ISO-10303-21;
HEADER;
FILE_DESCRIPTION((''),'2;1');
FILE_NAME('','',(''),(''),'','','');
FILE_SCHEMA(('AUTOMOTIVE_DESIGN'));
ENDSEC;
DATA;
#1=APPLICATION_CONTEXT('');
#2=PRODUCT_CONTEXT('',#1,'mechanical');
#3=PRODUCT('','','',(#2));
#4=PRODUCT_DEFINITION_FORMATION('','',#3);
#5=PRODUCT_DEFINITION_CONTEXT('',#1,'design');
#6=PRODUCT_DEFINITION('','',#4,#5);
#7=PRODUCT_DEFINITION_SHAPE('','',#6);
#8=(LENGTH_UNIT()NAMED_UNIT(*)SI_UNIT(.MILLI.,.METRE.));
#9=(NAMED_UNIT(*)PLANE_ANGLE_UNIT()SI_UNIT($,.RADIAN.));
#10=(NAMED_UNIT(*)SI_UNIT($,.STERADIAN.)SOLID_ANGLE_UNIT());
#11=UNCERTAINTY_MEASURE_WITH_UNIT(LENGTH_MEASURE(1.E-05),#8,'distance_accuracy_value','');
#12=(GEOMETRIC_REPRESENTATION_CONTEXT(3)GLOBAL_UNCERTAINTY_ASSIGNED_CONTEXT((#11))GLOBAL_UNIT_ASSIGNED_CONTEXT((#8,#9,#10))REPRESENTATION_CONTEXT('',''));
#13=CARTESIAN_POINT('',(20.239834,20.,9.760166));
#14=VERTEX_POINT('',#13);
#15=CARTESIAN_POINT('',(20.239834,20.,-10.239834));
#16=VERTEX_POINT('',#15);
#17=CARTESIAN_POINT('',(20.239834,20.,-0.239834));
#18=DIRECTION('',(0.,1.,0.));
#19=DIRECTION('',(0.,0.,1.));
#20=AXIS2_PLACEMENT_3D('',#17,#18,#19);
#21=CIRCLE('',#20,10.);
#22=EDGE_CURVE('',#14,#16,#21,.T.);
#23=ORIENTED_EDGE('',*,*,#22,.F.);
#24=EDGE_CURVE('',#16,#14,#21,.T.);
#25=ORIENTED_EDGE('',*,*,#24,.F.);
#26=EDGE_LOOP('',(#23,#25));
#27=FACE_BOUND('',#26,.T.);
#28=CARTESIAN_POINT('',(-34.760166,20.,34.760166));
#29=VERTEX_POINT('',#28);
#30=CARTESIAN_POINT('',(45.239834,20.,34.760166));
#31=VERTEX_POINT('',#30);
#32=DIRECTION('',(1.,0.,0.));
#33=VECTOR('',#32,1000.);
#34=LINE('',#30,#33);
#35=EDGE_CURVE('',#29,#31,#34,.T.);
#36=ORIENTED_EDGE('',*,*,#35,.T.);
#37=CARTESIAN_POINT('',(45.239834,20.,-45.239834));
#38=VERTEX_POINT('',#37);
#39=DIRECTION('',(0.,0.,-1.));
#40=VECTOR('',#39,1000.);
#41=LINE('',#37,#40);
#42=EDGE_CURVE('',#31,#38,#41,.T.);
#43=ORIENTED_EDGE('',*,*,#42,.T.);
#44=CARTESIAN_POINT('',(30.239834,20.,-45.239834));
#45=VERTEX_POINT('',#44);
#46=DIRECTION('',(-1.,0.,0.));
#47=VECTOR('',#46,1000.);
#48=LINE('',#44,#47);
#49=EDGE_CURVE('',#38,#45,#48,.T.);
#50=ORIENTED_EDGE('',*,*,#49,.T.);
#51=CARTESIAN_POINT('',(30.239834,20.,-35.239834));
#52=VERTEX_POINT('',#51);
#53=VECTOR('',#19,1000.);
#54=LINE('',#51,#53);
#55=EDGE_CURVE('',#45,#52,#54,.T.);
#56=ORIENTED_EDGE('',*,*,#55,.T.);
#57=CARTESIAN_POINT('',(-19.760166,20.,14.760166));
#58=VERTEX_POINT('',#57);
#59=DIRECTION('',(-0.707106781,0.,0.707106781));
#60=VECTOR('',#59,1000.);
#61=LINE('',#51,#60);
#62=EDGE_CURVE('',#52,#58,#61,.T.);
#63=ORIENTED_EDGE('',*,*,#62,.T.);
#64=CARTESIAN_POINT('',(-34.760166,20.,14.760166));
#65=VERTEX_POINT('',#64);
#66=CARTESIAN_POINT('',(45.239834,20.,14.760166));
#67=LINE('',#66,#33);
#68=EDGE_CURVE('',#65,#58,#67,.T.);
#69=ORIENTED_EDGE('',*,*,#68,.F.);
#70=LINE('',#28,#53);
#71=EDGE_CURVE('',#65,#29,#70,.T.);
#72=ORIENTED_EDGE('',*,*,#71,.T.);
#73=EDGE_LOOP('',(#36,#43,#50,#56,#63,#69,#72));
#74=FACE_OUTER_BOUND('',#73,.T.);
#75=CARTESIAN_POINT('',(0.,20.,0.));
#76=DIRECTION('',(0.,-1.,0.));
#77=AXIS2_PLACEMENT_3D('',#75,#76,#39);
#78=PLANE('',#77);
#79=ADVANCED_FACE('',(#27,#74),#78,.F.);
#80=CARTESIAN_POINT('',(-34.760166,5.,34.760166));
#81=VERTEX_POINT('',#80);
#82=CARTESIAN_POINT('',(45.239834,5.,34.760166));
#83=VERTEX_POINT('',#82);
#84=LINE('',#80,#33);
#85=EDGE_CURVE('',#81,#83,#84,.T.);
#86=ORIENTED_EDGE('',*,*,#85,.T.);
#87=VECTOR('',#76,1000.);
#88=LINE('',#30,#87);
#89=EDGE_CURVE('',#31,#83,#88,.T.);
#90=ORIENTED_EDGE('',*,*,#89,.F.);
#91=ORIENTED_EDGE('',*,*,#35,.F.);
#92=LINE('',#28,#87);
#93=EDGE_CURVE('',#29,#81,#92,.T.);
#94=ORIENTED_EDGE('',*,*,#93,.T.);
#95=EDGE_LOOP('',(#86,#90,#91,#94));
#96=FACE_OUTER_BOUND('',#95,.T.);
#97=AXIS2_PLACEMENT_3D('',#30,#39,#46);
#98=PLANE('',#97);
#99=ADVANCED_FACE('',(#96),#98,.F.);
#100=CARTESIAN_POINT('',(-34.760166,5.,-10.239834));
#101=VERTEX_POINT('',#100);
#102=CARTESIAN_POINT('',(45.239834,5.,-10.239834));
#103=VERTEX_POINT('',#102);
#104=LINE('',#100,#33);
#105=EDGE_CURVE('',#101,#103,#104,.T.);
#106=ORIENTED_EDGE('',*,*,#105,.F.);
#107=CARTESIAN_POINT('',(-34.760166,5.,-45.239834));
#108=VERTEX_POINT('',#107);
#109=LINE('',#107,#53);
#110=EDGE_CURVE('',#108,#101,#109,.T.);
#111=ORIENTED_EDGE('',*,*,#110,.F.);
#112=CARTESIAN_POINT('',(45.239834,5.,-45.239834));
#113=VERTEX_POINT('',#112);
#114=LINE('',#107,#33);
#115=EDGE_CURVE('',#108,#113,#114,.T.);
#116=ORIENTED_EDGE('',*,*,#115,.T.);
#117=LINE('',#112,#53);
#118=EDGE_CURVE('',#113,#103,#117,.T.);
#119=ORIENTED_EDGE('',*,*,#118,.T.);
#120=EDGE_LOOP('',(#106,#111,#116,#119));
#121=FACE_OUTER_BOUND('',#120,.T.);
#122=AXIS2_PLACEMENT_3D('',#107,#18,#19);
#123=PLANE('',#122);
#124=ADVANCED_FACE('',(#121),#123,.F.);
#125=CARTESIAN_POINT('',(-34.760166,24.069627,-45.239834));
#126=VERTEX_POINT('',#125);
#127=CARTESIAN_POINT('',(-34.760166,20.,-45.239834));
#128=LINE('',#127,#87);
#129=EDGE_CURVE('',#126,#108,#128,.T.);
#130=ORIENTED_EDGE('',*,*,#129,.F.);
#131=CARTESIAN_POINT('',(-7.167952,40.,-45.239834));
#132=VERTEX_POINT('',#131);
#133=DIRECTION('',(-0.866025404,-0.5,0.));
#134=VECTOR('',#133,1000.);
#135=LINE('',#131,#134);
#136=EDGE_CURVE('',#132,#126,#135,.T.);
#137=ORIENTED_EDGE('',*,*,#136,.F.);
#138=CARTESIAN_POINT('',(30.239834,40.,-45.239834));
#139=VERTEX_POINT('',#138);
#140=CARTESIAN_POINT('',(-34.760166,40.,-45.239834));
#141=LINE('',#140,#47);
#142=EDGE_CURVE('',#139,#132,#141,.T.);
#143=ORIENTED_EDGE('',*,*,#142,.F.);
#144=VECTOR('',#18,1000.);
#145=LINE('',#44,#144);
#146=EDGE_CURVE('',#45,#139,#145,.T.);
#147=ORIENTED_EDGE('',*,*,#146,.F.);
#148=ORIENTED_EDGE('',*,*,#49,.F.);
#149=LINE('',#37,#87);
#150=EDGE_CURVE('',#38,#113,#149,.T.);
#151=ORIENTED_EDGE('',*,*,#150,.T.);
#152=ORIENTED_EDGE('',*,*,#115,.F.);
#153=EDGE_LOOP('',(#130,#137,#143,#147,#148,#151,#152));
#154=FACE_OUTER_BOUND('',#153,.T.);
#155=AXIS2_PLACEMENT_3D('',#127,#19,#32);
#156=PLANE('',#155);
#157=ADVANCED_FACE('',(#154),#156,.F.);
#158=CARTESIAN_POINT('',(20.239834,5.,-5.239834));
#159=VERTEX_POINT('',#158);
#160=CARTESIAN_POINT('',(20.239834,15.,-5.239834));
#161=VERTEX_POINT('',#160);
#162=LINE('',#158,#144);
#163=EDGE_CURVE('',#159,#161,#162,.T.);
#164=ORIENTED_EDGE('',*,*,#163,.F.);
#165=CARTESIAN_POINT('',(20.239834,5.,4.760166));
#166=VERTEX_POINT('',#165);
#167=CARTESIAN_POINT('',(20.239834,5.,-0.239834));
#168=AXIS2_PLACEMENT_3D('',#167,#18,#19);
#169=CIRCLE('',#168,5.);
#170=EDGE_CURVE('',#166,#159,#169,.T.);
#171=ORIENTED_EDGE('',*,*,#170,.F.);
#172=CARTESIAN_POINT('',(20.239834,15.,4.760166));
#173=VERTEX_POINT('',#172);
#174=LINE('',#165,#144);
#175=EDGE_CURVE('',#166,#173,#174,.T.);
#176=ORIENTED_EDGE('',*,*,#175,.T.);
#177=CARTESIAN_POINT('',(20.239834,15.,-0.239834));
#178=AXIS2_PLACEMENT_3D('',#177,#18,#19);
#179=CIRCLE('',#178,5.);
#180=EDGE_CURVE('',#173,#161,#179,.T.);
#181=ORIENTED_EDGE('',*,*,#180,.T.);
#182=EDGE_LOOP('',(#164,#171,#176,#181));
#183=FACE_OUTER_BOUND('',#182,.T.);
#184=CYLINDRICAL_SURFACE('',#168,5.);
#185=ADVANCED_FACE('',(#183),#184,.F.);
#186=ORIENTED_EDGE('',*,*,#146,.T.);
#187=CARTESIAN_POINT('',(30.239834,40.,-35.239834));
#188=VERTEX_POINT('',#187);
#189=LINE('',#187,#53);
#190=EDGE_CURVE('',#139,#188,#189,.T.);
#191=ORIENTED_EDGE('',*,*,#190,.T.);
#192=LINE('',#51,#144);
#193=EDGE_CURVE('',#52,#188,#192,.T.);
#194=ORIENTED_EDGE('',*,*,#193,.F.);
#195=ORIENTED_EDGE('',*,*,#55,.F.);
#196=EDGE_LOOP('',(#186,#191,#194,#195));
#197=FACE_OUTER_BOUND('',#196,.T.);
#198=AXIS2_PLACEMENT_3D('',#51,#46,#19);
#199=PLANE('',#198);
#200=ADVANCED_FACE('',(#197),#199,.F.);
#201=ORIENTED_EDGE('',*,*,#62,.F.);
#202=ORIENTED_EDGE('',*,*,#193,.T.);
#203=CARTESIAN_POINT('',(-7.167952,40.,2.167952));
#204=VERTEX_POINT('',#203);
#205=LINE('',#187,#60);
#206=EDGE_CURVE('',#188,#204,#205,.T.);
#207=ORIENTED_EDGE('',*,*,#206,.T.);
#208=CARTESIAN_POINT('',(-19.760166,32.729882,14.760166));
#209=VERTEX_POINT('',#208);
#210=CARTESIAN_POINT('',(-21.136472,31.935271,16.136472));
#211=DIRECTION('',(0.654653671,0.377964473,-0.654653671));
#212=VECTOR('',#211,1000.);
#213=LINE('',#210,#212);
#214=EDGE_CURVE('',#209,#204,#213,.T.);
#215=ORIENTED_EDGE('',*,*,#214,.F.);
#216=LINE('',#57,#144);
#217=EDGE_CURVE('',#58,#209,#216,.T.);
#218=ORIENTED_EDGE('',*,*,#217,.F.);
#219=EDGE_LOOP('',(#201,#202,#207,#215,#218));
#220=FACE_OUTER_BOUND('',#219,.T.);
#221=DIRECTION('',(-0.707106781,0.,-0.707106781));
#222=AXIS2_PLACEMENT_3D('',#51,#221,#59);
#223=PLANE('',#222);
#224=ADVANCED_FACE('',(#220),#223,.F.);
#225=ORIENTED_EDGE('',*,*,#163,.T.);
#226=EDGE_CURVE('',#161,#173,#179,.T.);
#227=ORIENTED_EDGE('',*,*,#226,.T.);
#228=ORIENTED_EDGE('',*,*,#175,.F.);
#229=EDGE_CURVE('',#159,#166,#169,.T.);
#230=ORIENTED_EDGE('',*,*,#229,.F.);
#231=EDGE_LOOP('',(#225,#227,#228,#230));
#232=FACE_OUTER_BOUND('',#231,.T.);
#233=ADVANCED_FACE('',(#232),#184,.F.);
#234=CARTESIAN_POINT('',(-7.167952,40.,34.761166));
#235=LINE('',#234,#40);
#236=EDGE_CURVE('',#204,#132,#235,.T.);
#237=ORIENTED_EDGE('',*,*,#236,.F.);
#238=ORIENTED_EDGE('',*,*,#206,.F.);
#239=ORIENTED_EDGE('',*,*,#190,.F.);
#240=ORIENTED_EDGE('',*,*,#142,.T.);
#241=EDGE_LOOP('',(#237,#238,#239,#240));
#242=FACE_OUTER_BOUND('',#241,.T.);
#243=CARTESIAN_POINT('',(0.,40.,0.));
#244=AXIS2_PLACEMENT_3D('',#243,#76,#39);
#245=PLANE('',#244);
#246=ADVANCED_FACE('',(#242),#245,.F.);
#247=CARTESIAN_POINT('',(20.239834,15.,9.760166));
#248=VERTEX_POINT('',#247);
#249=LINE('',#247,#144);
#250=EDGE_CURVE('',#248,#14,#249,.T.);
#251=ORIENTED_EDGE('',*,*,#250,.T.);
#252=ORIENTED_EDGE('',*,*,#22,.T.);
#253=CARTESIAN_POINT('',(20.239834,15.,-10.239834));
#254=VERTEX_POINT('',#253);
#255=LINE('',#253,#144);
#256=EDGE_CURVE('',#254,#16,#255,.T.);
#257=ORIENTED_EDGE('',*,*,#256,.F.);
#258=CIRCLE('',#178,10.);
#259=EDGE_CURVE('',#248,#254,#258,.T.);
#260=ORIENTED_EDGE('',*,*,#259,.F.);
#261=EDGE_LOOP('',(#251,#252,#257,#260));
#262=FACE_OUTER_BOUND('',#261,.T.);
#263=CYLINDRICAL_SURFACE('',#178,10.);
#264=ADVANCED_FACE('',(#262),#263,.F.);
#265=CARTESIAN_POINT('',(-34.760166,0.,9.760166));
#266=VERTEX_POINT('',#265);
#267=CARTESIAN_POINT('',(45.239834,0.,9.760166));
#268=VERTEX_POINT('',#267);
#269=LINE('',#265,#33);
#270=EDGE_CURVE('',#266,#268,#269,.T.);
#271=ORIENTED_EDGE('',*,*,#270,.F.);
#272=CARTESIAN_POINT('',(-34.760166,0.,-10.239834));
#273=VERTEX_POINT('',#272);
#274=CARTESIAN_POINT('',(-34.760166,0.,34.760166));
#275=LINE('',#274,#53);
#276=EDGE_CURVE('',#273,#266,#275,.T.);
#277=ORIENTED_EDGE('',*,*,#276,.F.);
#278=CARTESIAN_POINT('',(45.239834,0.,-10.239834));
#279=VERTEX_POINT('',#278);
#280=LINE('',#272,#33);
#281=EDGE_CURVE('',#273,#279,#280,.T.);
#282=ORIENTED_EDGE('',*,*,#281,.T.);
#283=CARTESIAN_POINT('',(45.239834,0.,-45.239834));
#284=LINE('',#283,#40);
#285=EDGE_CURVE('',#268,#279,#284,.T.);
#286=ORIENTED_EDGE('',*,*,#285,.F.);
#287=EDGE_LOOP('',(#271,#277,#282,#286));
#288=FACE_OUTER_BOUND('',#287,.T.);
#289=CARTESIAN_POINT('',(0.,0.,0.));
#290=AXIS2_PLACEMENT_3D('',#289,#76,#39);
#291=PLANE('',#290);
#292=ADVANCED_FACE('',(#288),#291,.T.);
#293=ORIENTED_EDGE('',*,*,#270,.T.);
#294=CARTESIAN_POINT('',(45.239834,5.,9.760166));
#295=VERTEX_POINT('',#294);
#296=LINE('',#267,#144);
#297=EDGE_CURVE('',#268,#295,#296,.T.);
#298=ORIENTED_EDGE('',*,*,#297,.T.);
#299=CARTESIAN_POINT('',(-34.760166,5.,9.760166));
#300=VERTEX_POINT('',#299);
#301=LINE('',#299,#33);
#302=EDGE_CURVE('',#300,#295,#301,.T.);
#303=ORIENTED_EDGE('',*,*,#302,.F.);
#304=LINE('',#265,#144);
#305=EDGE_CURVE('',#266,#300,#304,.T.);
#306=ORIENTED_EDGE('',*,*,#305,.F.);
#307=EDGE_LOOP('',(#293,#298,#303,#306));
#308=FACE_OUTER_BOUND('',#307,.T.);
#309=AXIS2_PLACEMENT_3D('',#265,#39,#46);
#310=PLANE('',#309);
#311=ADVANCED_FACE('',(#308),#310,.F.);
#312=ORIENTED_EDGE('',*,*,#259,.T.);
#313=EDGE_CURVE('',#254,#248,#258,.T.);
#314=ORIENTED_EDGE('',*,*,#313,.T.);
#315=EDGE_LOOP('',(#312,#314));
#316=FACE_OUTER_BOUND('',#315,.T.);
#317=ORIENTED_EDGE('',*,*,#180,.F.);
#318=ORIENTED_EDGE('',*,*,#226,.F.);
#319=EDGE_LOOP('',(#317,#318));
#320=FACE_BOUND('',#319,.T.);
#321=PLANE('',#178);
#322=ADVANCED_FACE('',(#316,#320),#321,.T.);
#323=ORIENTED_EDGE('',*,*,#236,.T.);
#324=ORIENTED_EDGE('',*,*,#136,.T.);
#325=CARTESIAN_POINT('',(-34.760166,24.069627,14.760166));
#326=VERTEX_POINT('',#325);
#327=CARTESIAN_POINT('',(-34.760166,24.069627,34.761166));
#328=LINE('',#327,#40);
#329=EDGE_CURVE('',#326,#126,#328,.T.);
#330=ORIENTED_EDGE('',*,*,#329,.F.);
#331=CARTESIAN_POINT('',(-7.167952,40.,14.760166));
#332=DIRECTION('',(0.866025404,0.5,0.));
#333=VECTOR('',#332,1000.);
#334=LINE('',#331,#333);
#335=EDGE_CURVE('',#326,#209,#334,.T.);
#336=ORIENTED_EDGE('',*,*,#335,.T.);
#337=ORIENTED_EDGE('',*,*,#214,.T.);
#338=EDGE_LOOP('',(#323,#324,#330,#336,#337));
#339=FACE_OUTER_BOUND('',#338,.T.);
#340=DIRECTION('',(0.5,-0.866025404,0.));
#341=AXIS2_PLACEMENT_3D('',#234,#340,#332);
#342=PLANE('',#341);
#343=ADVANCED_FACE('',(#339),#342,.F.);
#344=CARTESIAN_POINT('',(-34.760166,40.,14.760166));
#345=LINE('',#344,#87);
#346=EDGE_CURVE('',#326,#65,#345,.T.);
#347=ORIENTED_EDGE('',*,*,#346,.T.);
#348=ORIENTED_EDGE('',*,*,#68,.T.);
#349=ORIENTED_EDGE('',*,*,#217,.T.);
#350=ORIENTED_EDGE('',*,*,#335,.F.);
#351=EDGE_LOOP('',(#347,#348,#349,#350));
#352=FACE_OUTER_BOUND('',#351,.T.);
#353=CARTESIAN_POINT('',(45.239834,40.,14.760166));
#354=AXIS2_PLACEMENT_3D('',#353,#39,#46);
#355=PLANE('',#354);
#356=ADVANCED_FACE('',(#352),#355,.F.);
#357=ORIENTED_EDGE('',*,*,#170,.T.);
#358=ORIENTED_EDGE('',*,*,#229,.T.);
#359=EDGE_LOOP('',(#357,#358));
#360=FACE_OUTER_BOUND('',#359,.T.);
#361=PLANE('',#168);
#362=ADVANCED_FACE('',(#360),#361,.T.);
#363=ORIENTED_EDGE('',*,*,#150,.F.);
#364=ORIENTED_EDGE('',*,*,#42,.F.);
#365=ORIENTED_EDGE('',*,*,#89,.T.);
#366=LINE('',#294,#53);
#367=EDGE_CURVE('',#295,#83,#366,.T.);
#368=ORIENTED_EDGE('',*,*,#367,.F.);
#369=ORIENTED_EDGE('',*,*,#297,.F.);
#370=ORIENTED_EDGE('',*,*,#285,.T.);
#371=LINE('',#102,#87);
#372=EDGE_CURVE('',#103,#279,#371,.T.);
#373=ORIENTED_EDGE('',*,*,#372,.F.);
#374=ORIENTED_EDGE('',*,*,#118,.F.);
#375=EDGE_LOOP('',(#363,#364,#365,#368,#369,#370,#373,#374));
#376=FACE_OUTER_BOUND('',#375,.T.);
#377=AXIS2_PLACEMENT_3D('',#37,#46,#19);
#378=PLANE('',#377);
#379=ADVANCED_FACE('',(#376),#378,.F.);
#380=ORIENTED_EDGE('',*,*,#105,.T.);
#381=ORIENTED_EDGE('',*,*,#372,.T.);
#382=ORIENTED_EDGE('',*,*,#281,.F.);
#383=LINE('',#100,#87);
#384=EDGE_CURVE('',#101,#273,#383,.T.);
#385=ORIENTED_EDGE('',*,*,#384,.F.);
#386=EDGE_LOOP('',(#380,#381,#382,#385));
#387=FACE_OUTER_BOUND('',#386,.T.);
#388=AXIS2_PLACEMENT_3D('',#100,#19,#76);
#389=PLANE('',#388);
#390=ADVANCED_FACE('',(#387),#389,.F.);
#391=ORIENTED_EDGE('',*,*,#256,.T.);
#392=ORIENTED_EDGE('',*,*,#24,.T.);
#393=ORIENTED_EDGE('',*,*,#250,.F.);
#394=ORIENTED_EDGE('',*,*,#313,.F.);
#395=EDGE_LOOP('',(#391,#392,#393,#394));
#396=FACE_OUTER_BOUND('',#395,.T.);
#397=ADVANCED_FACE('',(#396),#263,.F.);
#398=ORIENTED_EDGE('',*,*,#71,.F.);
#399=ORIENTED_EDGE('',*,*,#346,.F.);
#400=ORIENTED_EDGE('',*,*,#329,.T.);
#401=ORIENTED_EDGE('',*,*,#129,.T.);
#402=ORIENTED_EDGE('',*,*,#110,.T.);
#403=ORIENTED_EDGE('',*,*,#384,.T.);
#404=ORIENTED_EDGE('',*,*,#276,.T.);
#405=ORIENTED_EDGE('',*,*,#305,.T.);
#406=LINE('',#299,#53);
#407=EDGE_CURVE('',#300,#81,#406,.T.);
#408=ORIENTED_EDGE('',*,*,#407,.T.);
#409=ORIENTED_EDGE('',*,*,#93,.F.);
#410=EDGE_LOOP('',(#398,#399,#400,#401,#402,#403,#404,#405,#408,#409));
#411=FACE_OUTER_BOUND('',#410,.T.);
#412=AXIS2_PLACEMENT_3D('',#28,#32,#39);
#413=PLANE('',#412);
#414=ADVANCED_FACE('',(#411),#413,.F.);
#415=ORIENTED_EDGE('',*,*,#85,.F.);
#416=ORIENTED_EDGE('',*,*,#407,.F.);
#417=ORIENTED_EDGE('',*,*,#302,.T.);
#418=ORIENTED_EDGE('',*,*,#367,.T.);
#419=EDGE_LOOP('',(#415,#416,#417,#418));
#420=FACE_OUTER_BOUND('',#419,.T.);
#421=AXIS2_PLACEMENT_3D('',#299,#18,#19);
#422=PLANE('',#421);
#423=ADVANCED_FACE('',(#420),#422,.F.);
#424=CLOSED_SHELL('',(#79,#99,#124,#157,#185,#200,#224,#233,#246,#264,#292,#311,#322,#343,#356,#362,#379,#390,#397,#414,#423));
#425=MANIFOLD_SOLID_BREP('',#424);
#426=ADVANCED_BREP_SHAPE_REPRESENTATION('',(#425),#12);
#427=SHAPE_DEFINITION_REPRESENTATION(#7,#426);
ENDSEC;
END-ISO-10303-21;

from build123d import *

# Parameters (mm, degrees)
BASE_PLATE_SKETCH_W          = 80
BASE_PLATE_SKETCH_H          = 80
BASE_PLATE_80X80X20_DEPTH    = 20
BOTTOM_SLOT_SKETCH_W         = 25
BOTTOM_SLOT_SKETCH_H         = 5
BOTTOM_SLOT_SKETCH_W_2       = 35
BOTTOM_SLOT_DEPTH            = 80
RAISED_BLOCK_SKETCH_W        = 80
RAISED_BLOCK_SKETCH_H        = 60
RAISED_BLOCK_DEPTH           = 20
BLOCK_STEP_CUT_1_SKETCH_W    = 15
BLOCK_STEP_CUT_1_SKETCH_H    = 10
BLOCK_STEP_CUT_1_DEPTH       = 20
BLOCK_STEP_CUT_2_DEPTH       = 20
BLOCK_ANGLE_CUT_30DEG_REACH  = 102.233
COUNTERBORE_25_SKETCH_R      = 10
COUNTERBORE_25X5_DEPTH       = 5
HOLE_10_SKETCH_R             = 5
HOLE_10X10_DEPTH             = 10
AUXILIARY_BODY_EXTRUDE_DEPTH = 50
AUXILIARY_BODY_FILLET_R20_R  = 20


with BuildPart() as part:
    # Base Plate Sketch → Base Plate 80x80x20 (new body)
    with BuildSketch(Plane(origin=(0, 0, 0), x_dir=(1, 0, 0), z_dir=(0, 1, 0))):
        with Locations((5.239833721, 5.239833721)):
            Rectangle(BASE_PLATE_SKETCH_W, BASE_PLATE_SKETCH_H)
    extrude(amount=BASE_PLATE_80X80X20_DEPTH)

    # Bottom Slot Sketch → Bottom Slot (cut)
    with BuildSketch(Plane(origin=(45.239833721, 0, 0), x_dir=(0, 0, -1), z_dir=(1, 0, 0))):
        with Locations((-22.260166279, 2.5)):
            Rectangle(BOTTOM_SLOT_SKETCH_W, BOTTOM_SLOT_SKETCH_H)
        with Locations((27.739833721, 2.5)):
            Rectangle(BOTTOM_SLOT_SKETCH_W_2, BOTTOM_SLOT_SKETCH_H)
    extrude(amount=-BOTTOM_SLOT_DEPTH, mode=Mode.SUBTRACT)

    # Raised Block Sketch → Raised Block (add)
    with BuildSketch(Plane(origin=(0, 20, 0), x_dir=(1, 0, 0), z_dir=(0, 1, 0))):
        with Locations((5.239833721, 15.239833721)):
            Rectangle(RAISED_BLOCK_SKETCH_W, RAISED_BLOCK_SKETCH_H)
    extrude(amount=RAISED_BLOCK_DEPTH)

    # Block Step Cut 1 Sketch → Block Step Cut 1 (cut)
    with BuildSketch(Plane(origin=(0, 40, 0), x_dir=(1, 0, 0), z_dir=(0, 1, 0))):
        with Locations((37.739833721, 40.239833721)):
            Rectangle(BLOCK_STEP_CUT_1_SKETCH_W, BLOCK_STEP_CUT_1_SKETCH_H)
    extrude(amount=-BLOCK_STEP_CUT_1_DEPTH, mode=Mode.SUBTRACT)

    # Block Step Cut 2 Sketch → Block Step Cut 2 (cut)
    with BuildSketch(Plane(origin=(0, 40, 0), x_dir=(1, 0, 0), z_dir=(0, 1, 0))):
        Polygon((30.239833721, 35.239833721), (-19.760166279, -14.760166279), (45.239833721, -14.760166279), (45.239833721, 35.239833721), align=None)
    extrude(amount=-BLOCK_STEP_CUT_2_DEPTH, mode=Mode.SUBTRACT)

    # Block Angle Cut 30deg Sketch → Block Angle Cut 30deg (cut, up to next)
    with BuildSketch(Plane(origin=(0, 0, -45.239833721), x_dir=(-1, 0, 0), z_dir=(0, 0, -1)), mode=Mode.PRIVATE) as block_angle_cut_30deg_sk1:
        Polygon((34.760166279, 40), (7.167951709, 40), (34.760166279, 24.06962749), align=None)
    block_angle_cut_30deg_tool1 = extrude(block_angle_cut_30deg_sk1.sketch, amount=-BLOCK_ANGLE_CUT_30DEG_REACH, mode=Mode.PRIVATE) & part.part
    add(block_angle_cut_30deg_tool1.solids().sort_by_distance((-25.562761, 34.689876, -45.239834))[0], mode=Mode.SUBTRACT)

    # Counterbore Ø25 Sketch → Counterbore Ø25x5 (cut)
    with BuildSketch(Plane(origin=(0, 20, 0), x_dir=(1, 0, 0), z_dir=(0, 1, 0))):
        with Locations(Location((20.239833721, 0.239833721, 0), (0, 0, 270))):
            Circle(COUNTERBORE_25_SKETCH_R)
    extrude(amount=-COUNTERBORE_25X5_DEPTH, mode=Mode.SUBTRACT)

    # Hole Ø10 Sketch → Hole Ø10x10 (cut)
    with BuildSketch(Plane(origin=(0, 15, 0), x_dir=(1, 0, 0), z_dir=(0, 1, 0))):
        with Locations(Location((20.239833721, 0.239833721, 0), (0, 0, 270))):
            Circle(HOLE_10_SKETCH_R)
    extrude(amount=-HOLE_10X10_DEPTH, mode=Mode.SUBTRACT)


with BuildPart() as body_2:
    # Auxiliary Body Profile Sketch → Auxiliary Body Extrude (new, symmetric)
    with BuildSketch(Plane.XY):
        Polygon((417.503137043, -16.766117227), (417.503137043, -472.594475264), (451.565036325, -472.594475264), (451.565036325, -269.453576574), (494.657405519, -220.272068254), (589.816274586, -472.594475264), (625.881815002, -472.594475264), (519.87061451, -191.49612321), (672.967381657, -16.766117227), (635.900020673, -16.766117227), (451.565036325, -227.148436321), (451.565036325, -16.766117227), align=None)
    extrude(amount=AUXILIARY_BODY_EXTRUDE_DEPTH, both=True)

    # Auxiliary Body Fillet R20
    auxiliary_body_fillet_r20_edges = [body_2.edges().sort_by_distance(p)[0] for p in [
        (451.565036325, -227.148436321, 0),
        (519.87061451, -191.49612321, 0),
        (451.565036325, -269.453576574, 0),
    ]]
    fillet(auxiliary_body_fillet_r20_edges, radius=AUXILIARY_BODY_FILLET_R20_R)


solid = part.part
